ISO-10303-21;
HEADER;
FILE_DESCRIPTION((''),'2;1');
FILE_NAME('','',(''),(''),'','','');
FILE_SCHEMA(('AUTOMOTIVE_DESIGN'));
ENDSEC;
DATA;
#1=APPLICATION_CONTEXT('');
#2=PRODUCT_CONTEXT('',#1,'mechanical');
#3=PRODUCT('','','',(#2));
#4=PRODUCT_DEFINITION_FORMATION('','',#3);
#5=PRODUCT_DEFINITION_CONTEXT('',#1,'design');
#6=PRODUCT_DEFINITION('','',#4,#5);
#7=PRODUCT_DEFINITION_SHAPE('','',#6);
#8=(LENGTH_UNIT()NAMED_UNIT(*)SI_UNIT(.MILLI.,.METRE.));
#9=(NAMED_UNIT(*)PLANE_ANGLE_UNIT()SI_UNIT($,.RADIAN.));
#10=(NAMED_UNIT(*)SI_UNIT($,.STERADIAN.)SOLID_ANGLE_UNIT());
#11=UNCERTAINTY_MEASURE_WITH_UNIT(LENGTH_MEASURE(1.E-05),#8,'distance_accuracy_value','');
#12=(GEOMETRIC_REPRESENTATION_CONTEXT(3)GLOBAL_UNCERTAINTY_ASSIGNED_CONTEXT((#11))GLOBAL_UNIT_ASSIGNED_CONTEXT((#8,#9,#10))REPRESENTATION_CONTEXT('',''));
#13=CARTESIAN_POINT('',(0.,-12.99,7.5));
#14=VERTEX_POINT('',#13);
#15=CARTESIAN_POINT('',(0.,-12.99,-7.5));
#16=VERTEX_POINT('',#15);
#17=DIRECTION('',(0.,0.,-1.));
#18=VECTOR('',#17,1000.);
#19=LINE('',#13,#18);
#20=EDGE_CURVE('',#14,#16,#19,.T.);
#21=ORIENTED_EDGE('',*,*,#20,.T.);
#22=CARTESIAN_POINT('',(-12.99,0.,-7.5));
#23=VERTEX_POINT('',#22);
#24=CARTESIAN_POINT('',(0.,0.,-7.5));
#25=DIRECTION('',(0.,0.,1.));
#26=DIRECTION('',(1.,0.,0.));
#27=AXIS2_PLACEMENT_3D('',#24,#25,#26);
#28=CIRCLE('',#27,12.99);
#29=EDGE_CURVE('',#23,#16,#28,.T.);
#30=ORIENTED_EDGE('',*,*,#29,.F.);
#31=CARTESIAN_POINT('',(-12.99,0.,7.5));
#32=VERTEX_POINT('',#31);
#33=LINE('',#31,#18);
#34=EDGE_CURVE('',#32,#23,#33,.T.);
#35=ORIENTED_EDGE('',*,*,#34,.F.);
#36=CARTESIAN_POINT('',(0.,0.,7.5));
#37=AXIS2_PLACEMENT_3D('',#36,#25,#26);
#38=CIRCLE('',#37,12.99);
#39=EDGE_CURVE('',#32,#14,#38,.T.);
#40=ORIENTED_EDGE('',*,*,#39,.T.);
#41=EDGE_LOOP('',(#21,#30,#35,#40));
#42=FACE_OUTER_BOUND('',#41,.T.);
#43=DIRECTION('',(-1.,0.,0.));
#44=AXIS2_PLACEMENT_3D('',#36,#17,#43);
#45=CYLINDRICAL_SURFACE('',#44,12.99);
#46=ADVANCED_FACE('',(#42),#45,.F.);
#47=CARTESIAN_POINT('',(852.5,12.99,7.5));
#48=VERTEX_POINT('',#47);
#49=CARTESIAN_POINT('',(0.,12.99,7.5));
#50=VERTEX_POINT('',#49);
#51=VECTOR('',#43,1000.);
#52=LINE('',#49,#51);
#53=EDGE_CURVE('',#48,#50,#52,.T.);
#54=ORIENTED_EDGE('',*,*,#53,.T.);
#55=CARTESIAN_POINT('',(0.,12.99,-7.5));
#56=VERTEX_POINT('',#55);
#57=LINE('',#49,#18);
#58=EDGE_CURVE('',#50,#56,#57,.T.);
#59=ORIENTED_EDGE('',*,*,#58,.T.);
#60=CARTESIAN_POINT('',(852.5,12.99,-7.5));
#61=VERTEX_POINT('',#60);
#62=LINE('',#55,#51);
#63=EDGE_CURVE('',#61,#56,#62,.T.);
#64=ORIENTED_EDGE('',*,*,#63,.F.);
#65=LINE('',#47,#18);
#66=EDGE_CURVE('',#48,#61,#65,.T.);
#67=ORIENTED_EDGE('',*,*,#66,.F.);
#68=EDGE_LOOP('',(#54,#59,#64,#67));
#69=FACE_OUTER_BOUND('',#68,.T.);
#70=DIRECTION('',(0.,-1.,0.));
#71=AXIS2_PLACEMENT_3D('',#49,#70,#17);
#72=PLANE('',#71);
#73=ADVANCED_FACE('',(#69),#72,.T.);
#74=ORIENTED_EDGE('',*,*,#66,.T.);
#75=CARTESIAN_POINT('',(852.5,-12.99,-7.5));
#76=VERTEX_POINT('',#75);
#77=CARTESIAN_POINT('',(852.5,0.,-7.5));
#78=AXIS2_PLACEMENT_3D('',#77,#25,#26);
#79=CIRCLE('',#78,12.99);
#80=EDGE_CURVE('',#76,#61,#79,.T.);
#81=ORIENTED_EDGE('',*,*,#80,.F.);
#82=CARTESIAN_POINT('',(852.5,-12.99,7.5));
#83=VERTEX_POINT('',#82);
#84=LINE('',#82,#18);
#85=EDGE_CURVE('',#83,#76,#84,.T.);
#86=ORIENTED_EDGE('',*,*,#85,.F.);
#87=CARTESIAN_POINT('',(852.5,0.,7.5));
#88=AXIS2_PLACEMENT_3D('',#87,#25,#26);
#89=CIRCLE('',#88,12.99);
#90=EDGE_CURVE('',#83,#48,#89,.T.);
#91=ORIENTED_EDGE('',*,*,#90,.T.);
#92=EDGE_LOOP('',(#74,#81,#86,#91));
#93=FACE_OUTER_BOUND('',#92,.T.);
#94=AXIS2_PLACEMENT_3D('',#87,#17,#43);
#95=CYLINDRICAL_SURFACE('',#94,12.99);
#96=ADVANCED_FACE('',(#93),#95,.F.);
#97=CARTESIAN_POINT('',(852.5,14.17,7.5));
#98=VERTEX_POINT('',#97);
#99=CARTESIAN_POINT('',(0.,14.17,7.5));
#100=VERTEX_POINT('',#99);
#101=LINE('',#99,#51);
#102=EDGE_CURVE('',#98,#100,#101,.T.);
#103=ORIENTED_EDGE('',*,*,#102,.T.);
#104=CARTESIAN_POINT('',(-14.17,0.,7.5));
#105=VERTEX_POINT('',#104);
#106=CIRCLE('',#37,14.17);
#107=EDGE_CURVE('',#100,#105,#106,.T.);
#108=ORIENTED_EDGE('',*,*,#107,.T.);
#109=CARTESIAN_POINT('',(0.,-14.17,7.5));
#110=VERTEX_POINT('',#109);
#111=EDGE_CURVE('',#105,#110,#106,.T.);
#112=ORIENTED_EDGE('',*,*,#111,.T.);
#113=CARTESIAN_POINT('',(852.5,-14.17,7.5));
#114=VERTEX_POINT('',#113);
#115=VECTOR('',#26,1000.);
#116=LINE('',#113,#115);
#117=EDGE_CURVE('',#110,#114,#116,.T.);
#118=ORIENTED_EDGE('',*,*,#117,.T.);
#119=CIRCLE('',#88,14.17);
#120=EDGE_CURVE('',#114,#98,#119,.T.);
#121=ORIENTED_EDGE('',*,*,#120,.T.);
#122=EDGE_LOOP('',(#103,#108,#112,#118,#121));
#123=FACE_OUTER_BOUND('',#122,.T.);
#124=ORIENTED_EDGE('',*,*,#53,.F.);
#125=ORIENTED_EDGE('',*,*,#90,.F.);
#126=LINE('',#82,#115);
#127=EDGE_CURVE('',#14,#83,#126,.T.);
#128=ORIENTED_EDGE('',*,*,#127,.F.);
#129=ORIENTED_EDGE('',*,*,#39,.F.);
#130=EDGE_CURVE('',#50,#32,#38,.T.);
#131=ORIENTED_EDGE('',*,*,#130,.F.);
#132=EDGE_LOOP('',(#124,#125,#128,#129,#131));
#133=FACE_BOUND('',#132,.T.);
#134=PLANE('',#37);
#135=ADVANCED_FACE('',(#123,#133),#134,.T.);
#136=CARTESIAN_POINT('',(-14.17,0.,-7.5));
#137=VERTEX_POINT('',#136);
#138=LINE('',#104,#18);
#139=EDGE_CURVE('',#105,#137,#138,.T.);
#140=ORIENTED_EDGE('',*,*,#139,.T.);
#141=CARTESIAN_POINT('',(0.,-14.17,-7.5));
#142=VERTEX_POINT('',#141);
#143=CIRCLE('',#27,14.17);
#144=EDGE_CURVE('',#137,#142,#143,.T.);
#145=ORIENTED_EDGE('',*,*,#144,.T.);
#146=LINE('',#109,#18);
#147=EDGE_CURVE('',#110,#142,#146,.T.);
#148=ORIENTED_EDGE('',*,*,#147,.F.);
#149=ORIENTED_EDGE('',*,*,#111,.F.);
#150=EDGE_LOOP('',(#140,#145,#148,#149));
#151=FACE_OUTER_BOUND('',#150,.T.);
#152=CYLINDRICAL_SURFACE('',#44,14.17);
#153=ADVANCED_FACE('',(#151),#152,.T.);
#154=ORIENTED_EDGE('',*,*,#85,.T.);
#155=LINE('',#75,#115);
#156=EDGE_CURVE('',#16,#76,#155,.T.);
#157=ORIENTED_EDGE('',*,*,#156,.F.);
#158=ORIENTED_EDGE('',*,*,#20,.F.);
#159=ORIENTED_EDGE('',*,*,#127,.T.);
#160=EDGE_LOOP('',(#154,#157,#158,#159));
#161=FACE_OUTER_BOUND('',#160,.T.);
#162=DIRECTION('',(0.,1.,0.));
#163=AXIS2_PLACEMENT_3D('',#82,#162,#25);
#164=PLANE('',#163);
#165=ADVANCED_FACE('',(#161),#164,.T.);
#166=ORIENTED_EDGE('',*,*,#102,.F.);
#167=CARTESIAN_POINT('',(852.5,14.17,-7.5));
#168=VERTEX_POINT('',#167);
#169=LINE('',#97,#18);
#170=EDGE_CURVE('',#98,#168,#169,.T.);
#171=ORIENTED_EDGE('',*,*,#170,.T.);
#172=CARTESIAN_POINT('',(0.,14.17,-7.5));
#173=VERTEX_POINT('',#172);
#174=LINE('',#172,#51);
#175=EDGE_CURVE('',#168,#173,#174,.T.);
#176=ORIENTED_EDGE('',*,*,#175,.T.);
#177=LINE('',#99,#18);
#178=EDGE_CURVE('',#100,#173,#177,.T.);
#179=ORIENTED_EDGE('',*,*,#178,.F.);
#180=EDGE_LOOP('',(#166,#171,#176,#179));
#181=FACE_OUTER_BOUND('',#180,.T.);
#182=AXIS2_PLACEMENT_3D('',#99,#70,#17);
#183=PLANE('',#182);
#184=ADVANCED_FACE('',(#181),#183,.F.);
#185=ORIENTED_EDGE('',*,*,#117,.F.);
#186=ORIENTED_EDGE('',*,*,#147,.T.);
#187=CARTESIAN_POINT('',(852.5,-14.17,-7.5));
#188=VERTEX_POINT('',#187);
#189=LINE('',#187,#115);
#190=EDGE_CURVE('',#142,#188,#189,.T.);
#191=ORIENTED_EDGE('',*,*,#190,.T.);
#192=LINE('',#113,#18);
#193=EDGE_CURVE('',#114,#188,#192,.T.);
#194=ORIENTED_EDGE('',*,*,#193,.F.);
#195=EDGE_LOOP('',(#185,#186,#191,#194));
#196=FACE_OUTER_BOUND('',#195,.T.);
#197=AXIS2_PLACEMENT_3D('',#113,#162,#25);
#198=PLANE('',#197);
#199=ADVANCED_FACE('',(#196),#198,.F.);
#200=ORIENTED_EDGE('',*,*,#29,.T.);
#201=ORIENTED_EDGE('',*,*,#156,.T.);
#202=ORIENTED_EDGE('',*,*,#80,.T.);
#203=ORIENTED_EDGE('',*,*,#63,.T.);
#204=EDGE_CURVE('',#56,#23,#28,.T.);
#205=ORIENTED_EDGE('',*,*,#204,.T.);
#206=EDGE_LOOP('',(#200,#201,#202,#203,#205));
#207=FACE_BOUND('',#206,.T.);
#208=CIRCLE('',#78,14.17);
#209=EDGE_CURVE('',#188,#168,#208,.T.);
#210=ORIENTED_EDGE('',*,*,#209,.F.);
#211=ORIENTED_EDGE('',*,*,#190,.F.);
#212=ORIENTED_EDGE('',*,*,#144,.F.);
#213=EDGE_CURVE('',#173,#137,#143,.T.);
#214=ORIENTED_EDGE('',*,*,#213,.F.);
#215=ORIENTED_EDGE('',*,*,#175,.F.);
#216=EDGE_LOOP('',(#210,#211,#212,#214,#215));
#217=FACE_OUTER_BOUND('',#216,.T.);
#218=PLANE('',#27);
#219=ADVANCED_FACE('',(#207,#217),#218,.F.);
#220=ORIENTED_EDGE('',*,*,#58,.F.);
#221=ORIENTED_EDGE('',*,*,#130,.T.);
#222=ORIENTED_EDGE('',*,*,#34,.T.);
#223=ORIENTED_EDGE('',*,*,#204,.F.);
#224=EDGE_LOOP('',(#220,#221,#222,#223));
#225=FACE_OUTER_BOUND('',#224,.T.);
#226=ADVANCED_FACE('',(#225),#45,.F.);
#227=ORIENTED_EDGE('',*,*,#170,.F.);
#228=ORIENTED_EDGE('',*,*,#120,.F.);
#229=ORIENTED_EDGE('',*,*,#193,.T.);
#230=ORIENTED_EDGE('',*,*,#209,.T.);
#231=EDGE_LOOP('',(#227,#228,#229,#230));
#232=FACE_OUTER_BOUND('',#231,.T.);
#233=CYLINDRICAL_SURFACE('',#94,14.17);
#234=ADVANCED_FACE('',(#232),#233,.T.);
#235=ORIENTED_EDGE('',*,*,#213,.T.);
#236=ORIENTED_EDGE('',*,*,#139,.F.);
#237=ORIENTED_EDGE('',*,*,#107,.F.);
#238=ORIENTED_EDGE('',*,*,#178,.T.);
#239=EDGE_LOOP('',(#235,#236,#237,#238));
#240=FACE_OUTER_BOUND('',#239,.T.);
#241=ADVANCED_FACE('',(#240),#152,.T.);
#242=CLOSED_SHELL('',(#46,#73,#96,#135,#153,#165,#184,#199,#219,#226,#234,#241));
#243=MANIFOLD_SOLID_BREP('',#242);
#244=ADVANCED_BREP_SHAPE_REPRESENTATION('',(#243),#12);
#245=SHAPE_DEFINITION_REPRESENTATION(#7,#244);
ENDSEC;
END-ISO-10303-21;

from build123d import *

# Parameters (mm, degrees)
EXTRUDE_1_DEPTH = 7.5


with BuildPart() as part:
    # 草图1 → 凸台-拉伸1 (new, symmetric)
    with BuildSketch(Plane.XY):
        with BuildLine():
            Line((0, 14.17), (852.5, 14.17))
            ThreePointArc((852.5, 14.17), (866.67, 0), (852.5, -14.17))
            Line((852.5, -14.17), (0, -14.17))
            ThreePointArc((0, -14.17), (-14.17, 0), (0, 14.17))
        make_face()
        with BuildLine():
            Line((0, 12.99), (852.5, 12.99))
            ThreePointArc((852.5, 12.99), (865.49, 0), (852.5, -12.99))
            Line((852.5, -12.99), (0, -12.99))
            ThreePointArc((0, -12.99), (-12.99, 0), (0, 12.99))
        make_face(mode=Mode.SUBTRACT)
    extrude(amount=EXTRUDE_1_DEPTH, both=True)


solid = part.part
